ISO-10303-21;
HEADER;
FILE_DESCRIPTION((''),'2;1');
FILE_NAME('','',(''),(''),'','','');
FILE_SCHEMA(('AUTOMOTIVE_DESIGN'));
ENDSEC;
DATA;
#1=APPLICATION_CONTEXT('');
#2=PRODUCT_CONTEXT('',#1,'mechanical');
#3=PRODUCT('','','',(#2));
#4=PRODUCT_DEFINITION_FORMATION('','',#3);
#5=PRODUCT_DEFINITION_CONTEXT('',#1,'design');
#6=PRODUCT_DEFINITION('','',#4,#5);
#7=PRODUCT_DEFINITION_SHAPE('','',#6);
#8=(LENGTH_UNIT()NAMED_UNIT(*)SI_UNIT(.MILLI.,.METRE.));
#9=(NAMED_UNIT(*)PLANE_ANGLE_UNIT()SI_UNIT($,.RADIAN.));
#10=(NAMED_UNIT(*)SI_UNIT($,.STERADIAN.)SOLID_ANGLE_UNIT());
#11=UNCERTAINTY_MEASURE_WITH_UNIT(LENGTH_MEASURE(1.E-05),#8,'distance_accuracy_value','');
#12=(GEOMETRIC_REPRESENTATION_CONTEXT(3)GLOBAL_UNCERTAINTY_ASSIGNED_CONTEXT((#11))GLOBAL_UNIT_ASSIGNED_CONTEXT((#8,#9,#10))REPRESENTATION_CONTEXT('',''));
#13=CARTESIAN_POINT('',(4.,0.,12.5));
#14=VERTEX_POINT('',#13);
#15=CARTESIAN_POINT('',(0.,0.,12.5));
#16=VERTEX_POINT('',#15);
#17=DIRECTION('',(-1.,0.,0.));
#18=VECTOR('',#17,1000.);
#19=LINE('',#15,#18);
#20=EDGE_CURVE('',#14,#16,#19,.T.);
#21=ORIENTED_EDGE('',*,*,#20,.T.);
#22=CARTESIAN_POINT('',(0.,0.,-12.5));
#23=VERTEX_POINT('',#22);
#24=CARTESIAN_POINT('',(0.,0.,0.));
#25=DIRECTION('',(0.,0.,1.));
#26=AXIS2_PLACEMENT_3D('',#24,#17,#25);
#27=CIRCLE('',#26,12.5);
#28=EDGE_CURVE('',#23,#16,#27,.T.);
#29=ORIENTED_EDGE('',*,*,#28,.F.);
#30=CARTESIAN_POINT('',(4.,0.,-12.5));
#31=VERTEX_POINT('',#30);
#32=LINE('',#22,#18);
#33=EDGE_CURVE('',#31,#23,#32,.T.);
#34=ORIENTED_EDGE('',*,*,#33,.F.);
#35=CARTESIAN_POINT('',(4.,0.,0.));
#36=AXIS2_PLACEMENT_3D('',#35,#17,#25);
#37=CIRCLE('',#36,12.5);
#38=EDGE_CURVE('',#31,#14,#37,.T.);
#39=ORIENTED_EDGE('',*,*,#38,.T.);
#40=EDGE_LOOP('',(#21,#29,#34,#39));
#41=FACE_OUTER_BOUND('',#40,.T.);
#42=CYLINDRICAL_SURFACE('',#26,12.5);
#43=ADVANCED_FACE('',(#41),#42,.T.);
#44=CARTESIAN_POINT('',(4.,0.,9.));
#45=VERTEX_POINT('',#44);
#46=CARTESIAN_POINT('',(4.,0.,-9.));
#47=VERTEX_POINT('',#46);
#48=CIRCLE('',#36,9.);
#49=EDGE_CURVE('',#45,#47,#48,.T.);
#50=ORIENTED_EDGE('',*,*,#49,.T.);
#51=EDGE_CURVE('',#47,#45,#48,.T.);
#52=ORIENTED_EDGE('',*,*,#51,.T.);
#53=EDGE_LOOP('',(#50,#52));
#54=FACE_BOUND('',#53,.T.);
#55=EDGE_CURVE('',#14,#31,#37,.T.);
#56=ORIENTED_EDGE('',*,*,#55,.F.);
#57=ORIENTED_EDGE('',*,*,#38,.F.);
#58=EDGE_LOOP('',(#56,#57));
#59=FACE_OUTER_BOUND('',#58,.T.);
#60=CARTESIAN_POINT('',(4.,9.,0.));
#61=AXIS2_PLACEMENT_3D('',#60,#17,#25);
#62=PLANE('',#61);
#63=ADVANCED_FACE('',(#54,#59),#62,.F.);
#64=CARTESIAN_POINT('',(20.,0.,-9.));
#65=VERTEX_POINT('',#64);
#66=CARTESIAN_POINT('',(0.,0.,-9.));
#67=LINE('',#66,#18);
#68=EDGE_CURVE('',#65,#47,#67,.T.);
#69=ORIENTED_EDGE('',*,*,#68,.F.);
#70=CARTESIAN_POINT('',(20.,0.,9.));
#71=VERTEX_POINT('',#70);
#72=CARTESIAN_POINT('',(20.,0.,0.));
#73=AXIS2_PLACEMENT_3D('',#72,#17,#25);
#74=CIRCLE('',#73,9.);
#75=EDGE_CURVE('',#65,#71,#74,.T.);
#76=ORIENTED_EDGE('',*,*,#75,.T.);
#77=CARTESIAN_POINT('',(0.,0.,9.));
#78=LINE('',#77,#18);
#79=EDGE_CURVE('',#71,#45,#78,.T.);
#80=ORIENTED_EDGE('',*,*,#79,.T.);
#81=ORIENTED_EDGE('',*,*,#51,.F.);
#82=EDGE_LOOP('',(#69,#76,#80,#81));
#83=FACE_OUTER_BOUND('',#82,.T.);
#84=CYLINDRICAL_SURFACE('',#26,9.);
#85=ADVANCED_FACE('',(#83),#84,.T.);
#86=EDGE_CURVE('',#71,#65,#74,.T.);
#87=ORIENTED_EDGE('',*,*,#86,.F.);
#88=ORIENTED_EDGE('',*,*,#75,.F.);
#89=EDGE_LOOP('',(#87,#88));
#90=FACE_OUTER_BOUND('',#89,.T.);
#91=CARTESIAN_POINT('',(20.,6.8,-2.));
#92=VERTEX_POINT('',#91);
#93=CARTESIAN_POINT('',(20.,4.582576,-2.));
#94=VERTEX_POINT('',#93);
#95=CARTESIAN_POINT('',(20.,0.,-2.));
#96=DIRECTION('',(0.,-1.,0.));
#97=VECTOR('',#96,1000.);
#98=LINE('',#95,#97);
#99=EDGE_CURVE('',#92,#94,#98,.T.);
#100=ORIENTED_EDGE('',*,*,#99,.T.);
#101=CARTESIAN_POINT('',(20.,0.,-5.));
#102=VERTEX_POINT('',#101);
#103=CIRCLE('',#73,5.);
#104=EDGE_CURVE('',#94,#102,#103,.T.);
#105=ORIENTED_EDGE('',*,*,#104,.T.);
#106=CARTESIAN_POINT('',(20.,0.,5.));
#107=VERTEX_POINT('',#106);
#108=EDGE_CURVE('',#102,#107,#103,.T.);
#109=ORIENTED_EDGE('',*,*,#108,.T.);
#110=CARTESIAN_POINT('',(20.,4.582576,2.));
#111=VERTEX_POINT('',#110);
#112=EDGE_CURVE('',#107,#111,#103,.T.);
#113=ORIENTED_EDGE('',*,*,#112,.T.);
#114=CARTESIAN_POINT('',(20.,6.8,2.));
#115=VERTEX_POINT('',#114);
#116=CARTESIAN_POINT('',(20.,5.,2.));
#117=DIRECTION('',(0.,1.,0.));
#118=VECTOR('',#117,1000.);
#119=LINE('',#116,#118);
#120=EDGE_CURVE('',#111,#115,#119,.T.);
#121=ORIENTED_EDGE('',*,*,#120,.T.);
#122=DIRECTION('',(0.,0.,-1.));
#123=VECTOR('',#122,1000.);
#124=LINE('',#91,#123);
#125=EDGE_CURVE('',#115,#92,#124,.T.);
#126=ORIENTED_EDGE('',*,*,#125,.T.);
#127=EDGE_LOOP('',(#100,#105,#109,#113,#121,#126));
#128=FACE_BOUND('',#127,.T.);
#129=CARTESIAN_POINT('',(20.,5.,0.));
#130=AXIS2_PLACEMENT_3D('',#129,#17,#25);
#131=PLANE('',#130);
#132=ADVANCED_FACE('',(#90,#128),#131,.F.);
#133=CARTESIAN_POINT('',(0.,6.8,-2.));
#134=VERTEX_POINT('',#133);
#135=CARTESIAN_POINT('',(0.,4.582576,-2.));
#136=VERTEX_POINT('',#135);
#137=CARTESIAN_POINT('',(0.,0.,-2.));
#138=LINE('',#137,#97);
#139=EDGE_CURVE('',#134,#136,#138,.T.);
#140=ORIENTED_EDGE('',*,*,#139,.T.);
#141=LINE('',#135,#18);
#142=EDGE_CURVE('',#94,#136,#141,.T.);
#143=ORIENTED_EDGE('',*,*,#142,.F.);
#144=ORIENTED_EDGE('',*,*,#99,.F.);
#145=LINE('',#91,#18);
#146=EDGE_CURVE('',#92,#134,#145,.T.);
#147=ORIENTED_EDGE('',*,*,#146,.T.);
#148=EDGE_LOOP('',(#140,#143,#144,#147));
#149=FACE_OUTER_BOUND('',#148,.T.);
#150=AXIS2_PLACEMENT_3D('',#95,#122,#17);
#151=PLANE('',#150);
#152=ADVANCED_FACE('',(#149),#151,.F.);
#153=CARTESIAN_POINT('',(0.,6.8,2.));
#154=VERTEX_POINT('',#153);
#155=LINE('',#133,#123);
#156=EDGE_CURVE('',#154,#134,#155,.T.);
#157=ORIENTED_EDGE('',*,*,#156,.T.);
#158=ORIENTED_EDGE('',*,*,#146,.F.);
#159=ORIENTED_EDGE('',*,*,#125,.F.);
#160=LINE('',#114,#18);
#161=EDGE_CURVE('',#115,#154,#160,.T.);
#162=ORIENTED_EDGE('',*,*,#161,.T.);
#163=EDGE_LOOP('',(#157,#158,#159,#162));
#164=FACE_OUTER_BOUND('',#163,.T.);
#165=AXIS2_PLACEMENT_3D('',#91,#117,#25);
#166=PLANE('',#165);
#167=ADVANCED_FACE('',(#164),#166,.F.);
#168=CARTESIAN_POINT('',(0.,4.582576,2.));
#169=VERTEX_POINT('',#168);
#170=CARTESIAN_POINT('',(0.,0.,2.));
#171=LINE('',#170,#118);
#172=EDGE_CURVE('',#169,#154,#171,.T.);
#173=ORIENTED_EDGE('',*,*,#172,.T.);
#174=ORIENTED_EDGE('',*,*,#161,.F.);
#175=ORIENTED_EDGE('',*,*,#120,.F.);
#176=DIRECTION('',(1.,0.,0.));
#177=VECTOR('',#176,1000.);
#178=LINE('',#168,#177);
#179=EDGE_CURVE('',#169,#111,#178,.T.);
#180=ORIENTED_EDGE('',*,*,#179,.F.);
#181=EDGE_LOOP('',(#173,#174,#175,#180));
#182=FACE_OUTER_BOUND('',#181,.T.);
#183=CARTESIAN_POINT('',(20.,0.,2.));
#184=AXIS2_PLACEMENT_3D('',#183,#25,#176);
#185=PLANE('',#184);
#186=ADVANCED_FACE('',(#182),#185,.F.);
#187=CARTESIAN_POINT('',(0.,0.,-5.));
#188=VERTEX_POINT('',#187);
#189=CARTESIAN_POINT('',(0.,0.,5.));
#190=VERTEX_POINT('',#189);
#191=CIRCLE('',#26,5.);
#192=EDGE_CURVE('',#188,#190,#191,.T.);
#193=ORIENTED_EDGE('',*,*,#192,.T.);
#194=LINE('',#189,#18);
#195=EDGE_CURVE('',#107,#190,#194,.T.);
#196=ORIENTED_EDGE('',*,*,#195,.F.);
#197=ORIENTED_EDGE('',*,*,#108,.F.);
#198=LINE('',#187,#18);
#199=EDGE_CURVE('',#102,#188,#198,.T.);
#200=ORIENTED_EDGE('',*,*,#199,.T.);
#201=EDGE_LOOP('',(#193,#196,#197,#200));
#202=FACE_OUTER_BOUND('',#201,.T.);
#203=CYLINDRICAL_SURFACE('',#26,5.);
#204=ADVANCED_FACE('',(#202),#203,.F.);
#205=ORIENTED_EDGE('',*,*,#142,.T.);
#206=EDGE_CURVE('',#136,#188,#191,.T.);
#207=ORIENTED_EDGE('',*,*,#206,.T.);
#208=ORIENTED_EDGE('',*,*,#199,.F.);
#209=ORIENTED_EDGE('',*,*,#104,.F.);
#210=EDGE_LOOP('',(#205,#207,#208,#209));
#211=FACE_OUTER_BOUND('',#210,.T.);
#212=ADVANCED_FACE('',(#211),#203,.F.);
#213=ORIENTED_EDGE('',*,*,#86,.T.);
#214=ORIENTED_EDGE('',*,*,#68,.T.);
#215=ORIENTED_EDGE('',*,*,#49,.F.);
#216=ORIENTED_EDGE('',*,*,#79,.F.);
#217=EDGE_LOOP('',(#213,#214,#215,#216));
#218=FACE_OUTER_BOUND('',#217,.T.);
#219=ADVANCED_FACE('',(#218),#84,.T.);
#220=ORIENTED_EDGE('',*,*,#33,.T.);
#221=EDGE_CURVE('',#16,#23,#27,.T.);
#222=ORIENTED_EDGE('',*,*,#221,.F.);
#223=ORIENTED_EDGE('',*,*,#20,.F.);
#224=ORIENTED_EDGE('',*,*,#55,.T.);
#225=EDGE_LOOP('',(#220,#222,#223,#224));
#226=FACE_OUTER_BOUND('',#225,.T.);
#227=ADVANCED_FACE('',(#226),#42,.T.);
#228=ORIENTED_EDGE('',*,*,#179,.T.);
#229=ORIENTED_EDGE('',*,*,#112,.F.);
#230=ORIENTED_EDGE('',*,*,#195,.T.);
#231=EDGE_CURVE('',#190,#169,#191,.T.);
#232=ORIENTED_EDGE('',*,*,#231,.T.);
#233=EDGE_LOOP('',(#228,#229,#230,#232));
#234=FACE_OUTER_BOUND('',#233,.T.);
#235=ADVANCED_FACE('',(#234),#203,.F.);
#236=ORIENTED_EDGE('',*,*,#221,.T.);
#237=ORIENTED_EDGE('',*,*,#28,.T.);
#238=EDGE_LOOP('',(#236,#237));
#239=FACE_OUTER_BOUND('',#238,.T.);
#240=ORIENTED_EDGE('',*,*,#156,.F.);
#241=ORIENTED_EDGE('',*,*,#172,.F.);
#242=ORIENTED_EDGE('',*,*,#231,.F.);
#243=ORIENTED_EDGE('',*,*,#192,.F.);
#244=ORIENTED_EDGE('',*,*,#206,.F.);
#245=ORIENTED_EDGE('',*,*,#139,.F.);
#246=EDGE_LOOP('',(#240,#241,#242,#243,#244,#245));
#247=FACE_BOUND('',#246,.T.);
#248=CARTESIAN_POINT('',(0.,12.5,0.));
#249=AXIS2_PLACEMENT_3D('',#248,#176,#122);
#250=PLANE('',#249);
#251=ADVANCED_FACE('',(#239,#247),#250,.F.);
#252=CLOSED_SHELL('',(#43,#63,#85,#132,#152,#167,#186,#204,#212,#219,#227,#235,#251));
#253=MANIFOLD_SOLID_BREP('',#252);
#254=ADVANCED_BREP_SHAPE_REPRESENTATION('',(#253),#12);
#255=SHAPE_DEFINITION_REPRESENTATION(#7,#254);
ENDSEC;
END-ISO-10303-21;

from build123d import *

# Parameters (mm, degrees)
SKETCH_2_W          = 4
SKETCH_2_H          = 6.8
CUT_EXTRUDE_1_DEPTH = 27.69269563


with BuildPart() as part:
    # 草图1 → 旋转1 (revolve)
    with BuildSketch(Plane.XY, mode=Mode.PRIVATE) as revolve_1_sk:
        Polygon((0, 5), (20, 5), (20, 9), (4, 9), (4, 12.5), (0, 12.5), align=None)
    revolve(revolve_1_sk.sketch.rotate(Axis((0, 0, 0), (1, 0, 0)), 90), axis=Axis((0, 0, 0), (1, 0, 0)))

    # 草图2 → 切除-拉伸1 (cut, through all)
    with BuildSketch(Plane.ZY):
        with Locations((0, 3.4)):
            Rectangle(SKETCH_2_W, SKETCH_2_H)
    extrude(amount=-CUT_EXTRUDE_1_DEPTH, mode=Mode.SUBTRACT)


solid = part.part
